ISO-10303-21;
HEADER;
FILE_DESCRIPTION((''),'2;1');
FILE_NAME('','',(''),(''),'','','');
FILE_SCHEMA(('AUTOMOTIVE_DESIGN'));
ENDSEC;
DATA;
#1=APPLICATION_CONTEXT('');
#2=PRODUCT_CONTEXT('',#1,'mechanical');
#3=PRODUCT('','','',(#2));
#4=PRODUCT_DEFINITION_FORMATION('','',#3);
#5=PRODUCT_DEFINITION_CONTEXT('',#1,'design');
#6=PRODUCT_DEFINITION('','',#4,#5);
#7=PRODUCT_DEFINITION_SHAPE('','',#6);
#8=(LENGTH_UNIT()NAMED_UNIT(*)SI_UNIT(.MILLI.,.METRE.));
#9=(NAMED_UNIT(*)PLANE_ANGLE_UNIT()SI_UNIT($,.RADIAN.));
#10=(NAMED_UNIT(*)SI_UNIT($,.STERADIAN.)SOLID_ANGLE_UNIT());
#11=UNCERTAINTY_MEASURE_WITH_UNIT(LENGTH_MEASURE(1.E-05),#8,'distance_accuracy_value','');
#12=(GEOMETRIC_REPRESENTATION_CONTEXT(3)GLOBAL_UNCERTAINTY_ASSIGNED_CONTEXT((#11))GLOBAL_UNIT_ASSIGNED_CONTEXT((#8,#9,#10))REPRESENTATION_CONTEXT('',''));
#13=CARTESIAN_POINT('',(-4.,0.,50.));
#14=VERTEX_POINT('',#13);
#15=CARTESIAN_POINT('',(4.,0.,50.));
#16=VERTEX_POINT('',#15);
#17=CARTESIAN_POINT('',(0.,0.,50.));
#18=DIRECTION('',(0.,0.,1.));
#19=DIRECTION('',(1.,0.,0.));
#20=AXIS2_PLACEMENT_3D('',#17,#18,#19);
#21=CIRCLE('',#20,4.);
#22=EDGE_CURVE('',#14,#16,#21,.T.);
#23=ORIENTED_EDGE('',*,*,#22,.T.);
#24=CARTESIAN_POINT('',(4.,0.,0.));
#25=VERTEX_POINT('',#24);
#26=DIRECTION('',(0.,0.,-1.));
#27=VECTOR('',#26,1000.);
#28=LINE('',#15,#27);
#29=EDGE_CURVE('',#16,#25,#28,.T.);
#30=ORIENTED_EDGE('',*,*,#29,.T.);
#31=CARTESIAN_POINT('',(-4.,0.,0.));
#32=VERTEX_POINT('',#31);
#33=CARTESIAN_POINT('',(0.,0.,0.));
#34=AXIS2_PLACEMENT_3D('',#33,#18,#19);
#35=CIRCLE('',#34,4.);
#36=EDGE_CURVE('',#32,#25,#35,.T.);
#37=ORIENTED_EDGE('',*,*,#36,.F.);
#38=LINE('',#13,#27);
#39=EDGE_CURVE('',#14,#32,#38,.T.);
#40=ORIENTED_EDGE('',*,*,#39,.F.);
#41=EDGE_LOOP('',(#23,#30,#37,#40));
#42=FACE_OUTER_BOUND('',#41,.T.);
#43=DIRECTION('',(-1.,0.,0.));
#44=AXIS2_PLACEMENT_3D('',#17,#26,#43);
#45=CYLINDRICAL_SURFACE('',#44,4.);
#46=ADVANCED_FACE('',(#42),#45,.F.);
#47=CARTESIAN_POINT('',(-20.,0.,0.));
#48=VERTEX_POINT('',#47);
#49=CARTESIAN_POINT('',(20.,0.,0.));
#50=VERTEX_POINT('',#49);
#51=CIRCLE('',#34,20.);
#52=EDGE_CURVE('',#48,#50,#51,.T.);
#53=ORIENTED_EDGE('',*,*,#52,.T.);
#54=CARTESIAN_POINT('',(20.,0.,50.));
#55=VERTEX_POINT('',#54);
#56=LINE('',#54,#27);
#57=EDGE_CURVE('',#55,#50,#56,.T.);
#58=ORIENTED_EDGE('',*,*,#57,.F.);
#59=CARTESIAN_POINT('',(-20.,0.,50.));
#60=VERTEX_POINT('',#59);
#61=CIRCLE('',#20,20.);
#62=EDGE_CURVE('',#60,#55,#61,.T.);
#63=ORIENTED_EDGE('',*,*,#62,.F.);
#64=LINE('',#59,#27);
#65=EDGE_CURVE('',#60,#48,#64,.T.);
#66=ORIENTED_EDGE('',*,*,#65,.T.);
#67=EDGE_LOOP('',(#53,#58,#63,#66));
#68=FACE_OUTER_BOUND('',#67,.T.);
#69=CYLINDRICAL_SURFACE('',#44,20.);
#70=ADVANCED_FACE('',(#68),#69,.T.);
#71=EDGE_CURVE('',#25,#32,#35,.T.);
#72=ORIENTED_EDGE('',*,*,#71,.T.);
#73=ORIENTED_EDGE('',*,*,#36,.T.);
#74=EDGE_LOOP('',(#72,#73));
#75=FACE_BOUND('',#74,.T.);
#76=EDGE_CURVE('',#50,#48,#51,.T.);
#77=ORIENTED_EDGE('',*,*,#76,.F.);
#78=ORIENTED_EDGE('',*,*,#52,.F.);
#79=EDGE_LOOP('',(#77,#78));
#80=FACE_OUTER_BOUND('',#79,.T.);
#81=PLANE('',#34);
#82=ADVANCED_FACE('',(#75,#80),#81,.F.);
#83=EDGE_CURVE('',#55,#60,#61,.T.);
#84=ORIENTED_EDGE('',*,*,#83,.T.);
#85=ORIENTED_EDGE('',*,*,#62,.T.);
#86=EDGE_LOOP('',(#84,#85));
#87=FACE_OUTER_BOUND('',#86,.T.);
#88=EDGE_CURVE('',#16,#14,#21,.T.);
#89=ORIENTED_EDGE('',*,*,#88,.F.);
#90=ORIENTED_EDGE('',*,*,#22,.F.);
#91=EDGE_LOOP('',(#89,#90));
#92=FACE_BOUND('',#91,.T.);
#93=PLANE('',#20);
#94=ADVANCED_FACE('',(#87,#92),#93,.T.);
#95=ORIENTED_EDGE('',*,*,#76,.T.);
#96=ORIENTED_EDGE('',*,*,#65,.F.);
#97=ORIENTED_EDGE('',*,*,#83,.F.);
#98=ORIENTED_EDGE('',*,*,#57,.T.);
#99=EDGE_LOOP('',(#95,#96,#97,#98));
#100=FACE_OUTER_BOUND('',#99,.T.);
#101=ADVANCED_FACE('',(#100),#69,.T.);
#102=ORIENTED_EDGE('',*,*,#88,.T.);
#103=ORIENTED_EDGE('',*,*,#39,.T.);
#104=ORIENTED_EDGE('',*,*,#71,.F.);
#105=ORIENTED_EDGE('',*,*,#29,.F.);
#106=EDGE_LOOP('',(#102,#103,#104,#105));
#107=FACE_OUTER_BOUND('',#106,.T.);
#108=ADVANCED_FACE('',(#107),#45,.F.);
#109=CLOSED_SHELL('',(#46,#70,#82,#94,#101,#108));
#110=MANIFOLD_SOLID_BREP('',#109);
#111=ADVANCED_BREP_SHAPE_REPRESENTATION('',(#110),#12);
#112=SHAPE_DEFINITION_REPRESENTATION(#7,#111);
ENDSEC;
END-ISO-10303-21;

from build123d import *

# Parameters (mm, degrees)
SKETCH_1_R      = 20
SKETCH_1_R_2    = 4
EXTRUDE_1_DEPTH = 50


with BuildPart() as part:
    # 草图1 → 凸台-拉伸1 (new body)
    with BuildSketch(Plane.XY):
        Circle(SKETCH_1_R)
        Circle(SKETCH_1_R_2, mode=Mode.SUBTRACT)
    extrude(amount=EXTRUDE_1_DEPTH)


solid = part.part
